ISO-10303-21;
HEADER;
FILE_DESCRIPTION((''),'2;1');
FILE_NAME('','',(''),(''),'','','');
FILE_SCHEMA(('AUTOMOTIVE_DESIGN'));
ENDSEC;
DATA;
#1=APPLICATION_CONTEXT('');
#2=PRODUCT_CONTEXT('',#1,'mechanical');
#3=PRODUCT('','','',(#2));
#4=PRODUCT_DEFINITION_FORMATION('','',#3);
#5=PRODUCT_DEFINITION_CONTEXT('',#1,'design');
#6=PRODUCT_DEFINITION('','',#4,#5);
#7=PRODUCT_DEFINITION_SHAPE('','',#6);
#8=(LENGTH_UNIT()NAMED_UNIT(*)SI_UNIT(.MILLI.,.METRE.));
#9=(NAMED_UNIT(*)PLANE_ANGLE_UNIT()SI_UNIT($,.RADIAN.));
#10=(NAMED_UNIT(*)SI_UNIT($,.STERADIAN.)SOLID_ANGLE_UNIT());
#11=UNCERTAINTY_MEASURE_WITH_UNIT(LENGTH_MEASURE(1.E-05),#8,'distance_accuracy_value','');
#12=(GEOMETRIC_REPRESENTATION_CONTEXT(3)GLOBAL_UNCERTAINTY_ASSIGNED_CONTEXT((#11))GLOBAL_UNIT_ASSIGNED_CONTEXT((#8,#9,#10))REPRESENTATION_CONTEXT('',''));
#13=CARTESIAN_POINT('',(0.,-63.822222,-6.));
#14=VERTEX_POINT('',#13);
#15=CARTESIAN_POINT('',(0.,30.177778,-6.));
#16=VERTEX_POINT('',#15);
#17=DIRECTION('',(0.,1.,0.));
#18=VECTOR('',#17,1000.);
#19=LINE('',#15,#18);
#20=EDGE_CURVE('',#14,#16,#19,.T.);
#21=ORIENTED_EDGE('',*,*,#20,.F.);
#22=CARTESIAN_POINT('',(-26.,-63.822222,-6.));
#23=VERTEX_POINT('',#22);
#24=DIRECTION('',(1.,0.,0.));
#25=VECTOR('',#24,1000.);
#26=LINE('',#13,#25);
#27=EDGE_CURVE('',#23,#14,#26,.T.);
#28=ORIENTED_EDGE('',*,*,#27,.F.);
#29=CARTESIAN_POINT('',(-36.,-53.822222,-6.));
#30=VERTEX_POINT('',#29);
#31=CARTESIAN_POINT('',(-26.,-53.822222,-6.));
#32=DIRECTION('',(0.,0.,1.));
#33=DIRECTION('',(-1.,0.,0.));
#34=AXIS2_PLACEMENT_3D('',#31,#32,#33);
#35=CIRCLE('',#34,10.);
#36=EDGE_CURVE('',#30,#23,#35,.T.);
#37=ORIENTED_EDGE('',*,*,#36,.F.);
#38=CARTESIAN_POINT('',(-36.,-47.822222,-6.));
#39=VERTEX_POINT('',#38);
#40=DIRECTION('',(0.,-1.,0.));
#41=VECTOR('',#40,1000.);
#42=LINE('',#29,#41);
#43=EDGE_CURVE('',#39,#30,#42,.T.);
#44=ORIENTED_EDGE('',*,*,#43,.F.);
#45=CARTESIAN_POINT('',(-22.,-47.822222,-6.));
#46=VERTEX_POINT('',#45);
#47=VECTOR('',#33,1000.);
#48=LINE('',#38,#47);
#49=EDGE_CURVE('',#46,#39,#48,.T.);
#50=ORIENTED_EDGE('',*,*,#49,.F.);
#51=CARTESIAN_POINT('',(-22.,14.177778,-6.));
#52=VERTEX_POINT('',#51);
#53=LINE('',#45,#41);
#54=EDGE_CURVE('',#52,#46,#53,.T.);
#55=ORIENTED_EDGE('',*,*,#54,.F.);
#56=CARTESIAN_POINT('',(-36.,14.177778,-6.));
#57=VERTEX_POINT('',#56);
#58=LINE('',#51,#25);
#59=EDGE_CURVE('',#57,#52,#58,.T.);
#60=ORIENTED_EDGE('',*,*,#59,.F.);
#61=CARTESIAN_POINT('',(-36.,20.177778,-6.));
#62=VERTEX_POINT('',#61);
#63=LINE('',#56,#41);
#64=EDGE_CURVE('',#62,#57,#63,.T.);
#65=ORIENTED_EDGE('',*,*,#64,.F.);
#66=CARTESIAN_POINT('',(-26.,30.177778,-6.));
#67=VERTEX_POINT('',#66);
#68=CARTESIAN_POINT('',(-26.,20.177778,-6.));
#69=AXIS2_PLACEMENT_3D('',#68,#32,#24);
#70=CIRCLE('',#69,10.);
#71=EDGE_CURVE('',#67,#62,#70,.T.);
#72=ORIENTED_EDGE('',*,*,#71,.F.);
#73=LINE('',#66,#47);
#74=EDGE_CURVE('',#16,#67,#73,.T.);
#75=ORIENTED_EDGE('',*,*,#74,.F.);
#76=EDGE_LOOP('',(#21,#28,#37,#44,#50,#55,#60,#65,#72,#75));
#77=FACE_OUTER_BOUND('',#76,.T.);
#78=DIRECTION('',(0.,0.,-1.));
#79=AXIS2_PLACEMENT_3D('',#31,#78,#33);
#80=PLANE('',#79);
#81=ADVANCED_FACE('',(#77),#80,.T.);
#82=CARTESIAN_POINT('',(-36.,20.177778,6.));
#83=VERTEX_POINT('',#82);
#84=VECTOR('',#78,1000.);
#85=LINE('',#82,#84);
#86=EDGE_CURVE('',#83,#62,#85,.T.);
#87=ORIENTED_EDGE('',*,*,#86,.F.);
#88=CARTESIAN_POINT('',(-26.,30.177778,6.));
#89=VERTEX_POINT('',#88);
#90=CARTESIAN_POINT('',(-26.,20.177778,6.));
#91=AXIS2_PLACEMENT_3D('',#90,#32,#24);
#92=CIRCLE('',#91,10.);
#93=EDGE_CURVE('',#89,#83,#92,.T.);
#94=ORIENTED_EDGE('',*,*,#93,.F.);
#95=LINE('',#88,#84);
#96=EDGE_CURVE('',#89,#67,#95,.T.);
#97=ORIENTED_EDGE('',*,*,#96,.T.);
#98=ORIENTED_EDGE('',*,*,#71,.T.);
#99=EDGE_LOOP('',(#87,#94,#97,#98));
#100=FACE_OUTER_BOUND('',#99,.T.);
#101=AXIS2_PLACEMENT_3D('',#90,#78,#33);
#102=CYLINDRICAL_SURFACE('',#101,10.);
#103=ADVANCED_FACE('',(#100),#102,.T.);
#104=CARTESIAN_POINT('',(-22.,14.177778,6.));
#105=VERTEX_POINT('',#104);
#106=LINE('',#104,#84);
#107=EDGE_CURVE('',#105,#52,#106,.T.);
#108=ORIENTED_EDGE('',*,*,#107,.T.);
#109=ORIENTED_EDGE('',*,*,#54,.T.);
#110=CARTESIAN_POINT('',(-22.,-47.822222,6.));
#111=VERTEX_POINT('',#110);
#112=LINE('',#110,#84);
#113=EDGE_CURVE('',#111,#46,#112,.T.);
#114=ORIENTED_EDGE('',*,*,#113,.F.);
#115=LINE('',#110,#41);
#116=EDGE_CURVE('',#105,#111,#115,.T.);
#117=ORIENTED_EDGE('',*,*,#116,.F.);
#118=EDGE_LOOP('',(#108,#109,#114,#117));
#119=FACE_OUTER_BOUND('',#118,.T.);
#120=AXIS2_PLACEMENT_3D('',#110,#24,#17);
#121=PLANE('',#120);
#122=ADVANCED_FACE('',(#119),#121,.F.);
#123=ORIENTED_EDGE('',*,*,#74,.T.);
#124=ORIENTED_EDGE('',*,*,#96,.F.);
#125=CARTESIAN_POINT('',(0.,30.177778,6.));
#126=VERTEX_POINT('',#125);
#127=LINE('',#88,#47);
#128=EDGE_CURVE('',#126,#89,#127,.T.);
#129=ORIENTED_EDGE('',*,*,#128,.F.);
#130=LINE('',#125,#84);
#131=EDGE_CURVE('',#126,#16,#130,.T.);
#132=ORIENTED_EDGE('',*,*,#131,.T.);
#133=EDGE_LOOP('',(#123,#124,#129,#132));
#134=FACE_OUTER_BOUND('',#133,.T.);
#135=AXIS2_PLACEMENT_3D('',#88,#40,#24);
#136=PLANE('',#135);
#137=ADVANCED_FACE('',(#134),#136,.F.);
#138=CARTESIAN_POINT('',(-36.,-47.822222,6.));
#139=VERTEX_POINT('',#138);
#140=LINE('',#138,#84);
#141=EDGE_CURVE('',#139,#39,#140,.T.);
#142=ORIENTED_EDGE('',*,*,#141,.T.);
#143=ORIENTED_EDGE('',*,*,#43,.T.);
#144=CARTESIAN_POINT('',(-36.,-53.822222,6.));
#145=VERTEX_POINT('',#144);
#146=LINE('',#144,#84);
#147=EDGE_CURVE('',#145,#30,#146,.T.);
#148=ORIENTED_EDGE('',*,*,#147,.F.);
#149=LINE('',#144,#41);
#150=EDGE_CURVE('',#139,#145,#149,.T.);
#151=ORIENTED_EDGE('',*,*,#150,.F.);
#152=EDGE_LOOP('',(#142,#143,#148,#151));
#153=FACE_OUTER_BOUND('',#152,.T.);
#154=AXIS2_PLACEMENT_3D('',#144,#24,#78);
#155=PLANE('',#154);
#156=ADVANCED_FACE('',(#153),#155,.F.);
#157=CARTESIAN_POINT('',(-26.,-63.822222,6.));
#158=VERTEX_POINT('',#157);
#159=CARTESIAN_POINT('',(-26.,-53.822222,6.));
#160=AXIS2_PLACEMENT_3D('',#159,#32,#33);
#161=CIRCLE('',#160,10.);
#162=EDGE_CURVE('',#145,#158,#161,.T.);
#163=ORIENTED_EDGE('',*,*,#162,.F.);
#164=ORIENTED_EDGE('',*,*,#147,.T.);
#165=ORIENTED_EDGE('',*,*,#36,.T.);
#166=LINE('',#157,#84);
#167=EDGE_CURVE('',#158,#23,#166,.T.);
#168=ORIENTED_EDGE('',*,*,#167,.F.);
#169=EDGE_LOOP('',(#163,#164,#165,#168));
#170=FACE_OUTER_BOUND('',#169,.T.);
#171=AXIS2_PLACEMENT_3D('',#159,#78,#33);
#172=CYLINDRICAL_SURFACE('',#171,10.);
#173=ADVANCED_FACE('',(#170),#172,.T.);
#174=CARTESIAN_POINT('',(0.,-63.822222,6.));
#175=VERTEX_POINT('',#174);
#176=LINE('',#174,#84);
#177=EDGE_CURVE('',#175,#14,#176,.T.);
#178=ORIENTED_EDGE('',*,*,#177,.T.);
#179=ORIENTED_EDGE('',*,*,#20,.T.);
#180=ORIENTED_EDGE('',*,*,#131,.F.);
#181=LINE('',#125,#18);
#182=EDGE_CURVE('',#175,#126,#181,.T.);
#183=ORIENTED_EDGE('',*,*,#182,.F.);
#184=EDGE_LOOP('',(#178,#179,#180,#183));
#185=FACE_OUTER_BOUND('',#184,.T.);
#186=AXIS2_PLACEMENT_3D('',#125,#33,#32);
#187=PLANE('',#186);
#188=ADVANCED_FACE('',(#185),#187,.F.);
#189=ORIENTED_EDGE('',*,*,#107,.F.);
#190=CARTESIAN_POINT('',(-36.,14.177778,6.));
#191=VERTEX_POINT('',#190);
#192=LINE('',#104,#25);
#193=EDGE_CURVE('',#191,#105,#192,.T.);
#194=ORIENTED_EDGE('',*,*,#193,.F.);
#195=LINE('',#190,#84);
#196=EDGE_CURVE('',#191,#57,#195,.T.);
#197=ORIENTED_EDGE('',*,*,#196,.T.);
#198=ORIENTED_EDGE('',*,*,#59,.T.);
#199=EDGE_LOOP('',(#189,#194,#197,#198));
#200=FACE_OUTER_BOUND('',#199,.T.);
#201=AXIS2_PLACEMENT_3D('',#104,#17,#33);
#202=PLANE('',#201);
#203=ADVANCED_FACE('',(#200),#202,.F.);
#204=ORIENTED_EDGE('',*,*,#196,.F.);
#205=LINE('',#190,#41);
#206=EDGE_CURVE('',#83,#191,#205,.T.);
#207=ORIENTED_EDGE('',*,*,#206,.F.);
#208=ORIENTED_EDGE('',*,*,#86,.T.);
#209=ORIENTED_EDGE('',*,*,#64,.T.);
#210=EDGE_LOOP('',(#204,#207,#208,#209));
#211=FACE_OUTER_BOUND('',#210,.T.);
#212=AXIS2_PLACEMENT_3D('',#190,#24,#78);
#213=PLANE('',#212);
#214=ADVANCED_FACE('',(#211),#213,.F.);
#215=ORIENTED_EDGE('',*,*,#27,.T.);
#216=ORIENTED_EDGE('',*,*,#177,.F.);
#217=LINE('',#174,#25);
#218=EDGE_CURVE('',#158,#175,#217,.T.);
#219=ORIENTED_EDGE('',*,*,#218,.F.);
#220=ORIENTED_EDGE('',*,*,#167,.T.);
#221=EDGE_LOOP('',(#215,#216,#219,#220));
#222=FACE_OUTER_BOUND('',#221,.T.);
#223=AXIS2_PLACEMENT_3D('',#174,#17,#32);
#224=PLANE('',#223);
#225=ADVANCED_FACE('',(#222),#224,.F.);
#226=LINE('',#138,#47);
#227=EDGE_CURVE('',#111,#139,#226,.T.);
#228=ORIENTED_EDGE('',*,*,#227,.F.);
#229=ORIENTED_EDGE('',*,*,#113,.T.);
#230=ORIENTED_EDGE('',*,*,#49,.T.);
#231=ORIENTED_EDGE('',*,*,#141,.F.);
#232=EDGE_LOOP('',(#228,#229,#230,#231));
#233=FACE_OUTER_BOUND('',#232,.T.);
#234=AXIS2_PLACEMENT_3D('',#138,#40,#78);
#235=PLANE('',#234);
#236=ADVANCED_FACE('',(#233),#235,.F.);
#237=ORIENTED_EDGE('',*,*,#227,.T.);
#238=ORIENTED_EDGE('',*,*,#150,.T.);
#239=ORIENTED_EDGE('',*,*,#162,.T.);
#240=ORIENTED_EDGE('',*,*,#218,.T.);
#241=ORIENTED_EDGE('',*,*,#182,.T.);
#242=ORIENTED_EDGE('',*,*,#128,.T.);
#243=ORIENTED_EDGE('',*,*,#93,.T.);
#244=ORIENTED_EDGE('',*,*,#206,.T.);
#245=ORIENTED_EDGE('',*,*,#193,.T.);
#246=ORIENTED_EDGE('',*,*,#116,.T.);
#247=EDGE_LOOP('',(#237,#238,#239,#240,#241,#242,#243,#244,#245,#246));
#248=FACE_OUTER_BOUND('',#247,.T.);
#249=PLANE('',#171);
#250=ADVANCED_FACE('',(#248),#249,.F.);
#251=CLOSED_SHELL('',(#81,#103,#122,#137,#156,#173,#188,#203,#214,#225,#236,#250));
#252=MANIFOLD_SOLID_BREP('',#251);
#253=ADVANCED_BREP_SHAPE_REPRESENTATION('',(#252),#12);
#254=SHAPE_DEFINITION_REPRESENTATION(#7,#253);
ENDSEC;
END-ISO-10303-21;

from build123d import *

# Parameters (mm, degrees)
GIB_BODY_EXTRUDE_12MM_DEPTH = 6


with BuildPart() as part:
    # Gib Profile Sketch → Gib Body Extrude 12mm (new, symmetric)
    with BuildSketch(Plane.XY):
        with BuildLine():
            Line((-26, 30.177777778), (0, 30.177777778))
            Line((0, 30.177777778), (0, -63.822222222))
            Line((0, -63.822222222), (-26, -63.822222222))
            ThreePointArc((-26, -63.822222222), (-33.071067812, -60.893290034), (-36, -53.822222222))
            Line((-36, -53.822222222), (-36, -47.822222222))
            Line((-36, -47.822222222), (-22, -47.822222222))
            Line((-22, -47.822222222), (-22, 14.177777778))
            Line((-22, 14.177777778), (-36, 14.177777778))
            Line((-36, 14.177777778), (-36, 20.177777778))
            ThreePointArc((-36, 20.177777778), (-33.071067812, 27.24884559), (-26, 30.177777778))
        make_face()
    extrude(amount=GIB_BODY_EXTRUDE_12MM_DEPTH, both=True)


solid = part.part
